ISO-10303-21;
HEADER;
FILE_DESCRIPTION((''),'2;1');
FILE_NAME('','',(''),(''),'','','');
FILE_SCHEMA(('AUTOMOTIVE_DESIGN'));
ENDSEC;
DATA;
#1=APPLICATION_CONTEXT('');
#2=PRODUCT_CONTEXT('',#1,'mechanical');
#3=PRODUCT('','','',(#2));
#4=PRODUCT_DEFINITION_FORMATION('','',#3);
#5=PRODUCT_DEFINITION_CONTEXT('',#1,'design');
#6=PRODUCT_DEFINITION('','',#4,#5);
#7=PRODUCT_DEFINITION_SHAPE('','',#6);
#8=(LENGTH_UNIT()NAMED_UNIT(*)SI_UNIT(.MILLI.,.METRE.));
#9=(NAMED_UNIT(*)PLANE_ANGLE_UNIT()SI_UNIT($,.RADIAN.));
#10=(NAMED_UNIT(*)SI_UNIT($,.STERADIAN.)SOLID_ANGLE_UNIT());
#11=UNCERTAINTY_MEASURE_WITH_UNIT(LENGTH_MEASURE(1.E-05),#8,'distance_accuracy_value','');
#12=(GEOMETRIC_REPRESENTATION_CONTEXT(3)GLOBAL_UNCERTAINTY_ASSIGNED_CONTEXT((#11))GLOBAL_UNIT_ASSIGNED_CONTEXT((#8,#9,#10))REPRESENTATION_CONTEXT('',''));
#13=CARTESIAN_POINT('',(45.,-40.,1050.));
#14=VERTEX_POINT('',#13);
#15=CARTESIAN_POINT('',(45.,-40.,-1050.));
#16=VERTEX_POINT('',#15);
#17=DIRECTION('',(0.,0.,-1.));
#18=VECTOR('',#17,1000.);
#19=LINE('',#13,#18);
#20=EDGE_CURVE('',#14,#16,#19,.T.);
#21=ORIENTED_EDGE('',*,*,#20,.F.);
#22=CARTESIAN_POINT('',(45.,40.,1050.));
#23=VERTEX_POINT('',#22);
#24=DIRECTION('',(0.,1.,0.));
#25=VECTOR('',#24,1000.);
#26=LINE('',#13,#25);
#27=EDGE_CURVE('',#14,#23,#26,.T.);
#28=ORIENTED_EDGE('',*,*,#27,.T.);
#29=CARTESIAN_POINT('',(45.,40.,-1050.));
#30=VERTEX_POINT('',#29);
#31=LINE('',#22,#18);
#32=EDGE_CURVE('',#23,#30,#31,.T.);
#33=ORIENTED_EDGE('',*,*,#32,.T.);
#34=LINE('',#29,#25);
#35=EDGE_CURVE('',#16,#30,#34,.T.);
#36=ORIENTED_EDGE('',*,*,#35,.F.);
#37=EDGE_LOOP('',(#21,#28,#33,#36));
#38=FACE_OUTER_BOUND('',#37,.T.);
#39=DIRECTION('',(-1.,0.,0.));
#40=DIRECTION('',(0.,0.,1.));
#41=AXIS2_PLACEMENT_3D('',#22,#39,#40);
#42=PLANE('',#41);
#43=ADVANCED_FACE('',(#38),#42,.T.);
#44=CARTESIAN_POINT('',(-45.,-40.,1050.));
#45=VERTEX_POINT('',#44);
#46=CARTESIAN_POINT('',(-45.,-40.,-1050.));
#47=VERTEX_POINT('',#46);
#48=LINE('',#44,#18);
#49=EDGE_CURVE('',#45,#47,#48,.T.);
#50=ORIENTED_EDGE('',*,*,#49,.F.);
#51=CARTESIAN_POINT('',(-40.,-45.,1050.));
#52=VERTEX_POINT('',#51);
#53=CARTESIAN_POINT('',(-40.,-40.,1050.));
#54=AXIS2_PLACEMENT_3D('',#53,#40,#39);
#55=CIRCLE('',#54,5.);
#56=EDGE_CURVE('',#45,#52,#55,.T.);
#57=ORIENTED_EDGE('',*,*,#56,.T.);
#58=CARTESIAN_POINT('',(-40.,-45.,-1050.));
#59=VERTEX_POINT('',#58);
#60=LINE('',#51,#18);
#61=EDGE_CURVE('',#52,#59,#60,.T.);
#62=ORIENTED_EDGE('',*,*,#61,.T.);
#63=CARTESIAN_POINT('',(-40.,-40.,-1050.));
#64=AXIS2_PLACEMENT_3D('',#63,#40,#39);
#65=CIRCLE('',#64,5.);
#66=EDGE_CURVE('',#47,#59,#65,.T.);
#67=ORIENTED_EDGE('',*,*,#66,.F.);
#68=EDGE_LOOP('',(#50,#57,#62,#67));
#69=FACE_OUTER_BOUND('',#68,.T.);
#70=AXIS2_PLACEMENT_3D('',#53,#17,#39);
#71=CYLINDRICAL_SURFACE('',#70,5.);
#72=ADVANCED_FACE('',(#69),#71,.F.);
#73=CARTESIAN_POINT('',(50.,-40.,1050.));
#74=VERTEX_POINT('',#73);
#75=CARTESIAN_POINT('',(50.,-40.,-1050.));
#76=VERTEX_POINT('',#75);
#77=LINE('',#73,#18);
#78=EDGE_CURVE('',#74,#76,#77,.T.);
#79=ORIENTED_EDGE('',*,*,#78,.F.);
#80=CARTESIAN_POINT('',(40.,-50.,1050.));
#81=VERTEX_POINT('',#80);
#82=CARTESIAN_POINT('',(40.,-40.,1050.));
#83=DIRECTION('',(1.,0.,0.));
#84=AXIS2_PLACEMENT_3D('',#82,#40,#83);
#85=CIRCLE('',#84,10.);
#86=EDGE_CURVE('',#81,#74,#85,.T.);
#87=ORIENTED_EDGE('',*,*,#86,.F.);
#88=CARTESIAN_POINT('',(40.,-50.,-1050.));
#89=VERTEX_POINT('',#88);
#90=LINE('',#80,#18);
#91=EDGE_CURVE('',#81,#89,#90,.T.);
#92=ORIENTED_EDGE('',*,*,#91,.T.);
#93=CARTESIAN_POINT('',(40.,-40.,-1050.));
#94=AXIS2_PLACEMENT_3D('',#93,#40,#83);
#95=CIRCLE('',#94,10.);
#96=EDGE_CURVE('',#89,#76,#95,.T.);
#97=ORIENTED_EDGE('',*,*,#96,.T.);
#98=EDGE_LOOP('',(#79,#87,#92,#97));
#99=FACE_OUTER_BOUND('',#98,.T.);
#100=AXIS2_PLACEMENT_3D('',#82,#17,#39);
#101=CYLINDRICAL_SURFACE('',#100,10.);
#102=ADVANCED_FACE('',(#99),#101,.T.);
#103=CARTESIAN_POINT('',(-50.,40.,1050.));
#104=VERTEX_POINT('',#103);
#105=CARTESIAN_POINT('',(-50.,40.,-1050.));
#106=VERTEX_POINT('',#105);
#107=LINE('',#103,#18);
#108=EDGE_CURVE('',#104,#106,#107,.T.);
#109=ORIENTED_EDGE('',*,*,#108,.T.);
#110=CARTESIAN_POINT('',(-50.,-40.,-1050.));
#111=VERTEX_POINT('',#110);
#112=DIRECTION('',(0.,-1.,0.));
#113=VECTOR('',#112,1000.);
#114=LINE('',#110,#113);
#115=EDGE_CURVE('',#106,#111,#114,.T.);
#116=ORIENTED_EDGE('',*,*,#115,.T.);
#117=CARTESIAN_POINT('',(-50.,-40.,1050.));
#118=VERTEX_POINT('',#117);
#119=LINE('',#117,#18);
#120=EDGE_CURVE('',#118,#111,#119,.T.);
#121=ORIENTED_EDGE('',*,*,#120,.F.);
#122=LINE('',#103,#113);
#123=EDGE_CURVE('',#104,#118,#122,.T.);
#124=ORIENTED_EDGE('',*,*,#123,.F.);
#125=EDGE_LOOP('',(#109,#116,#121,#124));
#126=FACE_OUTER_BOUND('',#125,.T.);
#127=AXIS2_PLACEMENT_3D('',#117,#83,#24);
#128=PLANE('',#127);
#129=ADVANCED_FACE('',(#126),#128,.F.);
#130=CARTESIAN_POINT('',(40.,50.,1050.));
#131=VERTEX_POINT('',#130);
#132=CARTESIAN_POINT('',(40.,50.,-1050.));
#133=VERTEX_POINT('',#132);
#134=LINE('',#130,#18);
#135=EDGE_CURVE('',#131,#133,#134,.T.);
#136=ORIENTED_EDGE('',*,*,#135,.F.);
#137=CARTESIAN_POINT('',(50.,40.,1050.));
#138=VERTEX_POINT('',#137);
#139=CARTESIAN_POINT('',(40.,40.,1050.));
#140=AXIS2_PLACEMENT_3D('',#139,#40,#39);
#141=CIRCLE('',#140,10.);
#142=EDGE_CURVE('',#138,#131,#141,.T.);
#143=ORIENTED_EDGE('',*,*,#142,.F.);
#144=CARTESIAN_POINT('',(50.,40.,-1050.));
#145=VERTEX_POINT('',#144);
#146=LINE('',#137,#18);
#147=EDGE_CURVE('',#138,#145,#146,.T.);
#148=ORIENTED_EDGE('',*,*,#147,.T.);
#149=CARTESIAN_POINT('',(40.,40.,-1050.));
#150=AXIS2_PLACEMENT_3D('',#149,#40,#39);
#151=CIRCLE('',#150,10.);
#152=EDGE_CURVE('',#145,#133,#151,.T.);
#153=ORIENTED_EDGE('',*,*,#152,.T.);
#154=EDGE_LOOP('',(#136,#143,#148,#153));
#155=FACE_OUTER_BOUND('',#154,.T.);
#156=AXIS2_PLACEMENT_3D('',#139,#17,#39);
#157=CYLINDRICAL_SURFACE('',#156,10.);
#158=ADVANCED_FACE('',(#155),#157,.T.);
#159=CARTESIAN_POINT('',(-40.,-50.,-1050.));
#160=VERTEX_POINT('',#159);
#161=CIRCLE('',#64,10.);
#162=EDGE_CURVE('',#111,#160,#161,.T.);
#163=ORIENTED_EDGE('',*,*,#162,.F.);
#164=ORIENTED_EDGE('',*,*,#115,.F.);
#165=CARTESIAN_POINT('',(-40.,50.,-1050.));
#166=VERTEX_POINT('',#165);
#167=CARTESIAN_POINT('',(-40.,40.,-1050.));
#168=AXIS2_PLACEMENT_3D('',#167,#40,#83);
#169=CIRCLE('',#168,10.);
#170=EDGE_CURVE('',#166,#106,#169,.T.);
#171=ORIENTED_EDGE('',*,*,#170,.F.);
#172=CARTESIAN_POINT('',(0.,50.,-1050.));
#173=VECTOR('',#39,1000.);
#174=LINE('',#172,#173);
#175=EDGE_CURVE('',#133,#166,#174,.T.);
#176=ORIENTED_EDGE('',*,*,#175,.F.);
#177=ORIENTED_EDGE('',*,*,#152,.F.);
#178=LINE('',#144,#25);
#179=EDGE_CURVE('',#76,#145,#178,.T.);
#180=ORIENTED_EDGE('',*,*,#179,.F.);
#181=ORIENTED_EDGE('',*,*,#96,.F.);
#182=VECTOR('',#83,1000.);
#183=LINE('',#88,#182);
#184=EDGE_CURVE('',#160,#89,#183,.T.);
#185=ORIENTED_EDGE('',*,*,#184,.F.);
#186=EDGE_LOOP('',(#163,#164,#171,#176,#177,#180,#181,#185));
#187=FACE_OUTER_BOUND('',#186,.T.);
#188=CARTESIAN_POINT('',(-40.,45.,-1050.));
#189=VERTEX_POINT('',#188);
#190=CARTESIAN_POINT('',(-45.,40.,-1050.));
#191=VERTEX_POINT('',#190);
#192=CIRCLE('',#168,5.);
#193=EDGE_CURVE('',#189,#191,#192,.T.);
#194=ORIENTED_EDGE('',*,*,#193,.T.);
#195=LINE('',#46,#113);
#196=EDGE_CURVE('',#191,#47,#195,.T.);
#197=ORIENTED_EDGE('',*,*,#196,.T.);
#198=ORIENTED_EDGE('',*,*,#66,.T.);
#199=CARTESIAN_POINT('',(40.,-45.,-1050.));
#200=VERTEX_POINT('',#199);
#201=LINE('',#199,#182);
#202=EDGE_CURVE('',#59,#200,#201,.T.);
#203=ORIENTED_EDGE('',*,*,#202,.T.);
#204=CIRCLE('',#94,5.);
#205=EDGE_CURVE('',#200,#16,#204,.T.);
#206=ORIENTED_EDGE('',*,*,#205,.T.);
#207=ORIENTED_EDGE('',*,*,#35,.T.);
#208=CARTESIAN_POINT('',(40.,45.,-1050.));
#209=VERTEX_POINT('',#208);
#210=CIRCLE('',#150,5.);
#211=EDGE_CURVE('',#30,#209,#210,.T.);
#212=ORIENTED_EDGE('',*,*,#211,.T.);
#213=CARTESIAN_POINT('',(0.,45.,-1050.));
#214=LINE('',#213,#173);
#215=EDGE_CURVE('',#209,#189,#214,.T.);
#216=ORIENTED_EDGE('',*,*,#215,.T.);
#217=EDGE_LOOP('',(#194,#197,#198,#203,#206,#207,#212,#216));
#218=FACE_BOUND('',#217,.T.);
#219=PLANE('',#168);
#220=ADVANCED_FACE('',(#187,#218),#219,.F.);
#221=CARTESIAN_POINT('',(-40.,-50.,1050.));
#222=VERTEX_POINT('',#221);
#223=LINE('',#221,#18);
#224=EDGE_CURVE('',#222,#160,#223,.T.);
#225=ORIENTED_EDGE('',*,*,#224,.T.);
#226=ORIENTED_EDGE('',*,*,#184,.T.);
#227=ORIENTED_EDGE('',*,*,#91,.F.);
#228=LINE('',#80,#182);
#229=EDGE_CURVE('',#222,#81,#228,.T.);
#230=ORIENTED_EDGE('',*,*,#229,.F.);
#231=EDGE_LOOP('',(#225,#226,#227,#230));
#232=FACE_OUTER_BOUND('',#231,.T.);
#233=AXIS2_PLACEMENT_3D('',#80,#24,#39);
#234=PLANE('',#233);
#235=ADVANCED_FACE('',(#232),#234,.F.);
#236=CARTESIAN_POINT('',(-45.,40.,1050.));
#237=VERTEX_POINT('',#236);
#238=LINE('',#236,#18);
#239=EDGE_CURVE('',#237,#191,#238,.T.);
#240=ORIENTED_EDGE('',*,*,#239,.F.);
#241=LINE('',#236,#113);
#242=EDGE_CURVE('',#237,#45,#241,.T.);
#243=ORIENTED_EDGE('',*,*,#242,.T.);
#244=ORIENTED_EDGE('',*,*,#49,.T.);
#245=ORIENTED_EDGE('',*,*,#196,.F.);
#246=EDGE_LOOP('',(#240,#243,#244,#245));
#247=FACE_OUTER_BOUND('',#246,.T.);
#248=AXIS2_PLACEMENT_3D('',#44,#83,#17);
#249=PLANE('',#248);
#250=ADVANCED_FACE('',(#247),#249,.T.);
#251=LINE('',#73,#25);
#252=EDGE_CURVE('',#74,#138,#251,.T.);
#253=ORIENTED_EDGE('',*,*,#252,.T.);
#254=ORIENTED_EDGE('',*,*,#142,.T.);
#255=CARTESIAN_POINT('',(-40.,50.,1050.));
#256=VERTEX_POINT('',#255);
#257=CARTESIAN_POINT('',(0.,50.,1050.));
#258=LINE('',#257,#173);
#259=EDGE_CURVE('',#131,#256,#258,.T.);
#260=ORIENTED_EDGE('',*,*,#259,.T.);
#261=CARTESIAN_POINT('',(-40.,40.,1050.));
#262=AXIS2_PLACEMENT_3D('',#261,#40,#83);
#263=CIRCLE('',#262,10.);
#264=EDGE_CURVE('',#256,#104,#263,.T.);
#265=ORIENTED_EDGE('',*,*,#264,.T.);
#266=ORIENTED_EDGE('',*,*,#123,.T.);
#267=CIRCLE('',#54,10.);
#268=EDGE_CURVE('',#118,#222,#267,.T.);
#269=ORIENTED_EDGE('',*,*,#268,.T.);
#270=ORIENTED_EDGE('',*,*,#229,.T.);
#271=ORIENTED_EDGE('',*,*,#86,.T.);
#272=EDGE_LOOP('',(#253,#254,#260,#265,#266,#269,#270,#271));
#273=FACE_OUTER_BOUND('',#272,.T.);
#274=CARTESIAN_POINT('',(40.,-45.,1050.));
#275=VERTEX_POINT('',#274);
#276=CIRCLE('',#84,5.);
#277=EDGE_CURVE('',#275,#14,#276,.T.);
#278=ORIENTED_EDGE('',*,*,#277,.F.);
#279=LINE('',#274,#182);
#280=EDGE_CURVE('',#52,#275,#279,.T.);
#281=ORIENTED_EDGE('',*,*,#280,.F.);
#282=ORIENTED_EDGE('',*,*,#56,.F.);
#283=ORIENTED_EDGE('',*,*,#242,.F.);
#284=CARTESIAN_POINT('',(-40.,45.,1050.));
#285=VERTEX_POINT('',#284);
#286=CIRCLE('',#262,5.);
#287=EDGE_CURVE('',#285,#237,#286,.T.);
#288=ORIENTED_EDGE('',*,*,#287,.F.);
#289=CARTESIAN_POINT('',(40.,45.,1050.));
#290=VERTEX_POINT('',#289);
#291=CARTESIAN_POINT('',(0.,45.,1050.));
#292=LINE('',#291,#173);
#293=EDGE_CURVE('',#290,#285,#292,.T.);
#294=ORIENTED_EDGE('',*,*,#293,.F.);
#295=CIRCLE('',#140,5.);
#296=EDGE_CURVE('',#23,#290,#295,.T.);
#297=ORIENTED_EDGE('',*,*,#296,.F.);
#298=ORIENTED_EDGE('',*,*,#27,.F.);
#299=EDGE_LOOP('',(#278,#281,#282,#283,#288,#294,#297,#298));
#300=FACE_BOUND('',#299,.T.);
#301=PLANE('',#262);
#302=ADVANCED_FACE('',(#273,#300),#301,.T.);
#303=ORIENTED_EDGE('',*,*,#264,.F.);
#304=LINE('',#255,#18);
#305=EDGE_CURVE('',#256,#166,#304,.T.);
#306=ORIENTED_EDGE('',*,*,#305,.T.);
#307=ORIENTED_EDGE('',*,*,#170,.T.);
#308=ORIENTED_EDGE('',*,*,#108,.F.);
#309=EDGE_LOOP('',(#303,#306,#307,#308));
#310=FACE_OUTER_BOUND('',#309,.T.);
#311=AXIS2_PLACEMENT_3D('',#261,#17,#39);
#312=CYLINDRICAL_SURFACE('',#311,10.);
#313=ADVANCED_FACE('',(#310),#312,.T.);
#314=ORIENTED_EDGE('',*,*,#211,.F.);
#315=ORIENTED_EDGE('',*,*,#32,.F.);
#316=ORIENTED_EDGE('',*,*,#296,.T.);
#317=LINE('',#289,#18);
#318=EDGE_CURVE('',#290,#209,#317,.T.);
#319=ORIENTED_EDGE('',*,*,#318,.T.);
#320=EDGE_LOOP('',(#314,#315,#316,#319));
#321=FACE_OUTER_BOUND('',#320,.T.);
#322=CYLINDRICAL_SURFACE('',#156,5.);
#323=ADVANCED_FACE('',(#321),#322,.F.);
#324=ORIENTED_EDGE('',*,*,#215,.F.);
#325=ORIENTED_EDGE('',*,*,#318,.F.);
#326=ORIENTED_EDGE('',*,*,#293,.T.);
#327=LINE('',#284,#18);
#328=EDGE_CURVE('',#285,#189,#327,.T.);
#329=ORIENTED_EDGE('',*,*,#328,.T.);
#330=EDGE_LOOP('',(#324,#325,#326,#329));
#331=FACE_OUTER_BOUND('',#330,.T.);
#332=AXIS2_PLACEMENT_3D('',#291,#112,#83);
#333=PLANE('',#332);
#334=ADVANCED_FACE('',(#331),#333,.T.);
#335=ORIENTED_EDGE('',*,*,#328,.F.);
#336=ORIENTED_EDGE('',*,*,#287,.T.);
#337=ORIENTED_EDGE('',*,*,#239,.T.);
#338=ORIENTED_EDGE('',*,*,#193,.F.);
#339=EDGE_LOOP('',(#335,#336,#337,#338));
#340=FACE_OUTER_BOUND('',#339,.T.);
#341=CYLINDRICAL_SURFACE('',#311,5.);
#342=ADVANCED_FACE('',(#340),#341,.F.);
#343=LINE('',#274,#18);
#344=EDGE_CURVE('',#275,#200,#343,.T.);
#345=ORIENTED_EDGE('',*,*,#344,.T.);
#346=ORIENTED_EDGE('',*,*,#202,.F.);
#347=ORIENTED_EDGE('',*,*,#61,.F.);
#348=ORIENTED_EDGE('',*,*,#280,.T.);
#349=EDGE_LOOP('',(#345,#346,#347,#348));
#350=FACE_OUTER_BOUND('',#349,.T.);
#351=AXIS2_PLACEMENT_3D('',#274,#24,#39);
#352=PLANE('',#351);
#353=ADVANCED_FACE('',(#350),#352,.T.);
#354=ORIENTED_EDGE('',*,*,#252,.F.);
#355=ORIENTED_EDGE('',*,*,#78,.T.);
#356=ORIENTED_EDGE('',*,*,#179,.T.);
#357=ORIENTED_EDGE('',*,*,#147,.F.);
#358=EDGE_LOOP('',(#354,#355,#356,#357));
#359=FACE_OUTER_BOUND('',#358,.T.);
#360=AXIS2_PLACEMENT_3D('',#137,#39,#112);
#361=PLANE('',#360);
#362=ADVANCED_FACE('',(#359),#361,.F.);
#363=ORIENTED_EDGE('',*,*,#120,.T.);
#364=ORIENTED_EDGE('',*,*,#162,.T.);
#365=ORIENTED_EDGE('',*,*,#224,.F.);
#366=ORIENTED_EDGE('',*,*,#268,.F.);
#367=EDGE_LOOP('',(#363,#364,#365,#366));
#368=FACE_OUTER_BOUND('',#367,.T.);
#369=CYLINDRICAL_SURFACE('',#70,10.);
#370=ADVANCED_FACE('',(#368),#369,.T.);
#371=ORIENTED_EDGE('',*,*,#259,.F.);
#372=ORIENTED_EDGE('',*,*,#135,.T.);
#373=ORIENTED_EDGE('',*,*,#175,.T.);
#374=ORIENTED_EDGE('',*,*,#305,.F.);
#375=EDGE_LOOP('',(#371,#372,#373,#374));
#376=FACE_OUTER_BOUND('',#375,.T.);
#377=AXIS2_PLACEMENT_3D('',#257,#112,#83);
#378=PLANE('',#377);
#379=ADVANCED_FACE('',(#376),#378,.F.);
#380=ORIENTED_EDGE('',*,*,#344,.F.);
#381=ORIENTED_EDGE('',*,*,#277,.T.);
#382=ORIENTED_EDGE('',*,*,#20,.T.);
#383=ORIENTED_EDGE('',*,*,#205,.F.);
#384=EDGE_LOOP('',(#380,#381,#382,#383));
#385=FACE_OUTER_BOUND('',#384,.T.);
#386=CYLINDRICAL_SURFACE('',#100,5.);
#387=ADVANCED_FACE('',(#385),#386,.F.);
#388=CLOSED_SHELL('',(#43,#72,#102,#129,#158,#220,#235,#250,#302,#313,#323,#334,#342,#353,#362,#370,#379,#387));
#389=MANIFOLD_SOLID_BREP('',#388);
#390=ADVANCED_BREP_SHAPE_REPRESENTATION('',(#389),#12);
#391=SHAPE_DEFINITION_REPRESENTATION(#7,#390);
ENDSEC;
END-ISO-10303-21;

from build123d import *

# Parameters (mm, degrees)
BOSS_EXTRUDE_1_DEPTH = 1050


with BuildPart() as part:
    # Sketch 1 → Boss-Extrude 1 (new, symmetric)
    with BuildSketch(Plane.XY):
        with BuildLine():
            Line((0, 50), (-40, 50))
            ThreePointArc((-40, 50), (-47.071067812, 47.071067812), (-50, 40))
            Line((-50, 40), (-50, 0))
            Line((-50, 0), (-50, -40))
            ThreePointArc((-50, -40), (-47.071067812, -47.071067812), (-40, -50))
            Line((-40, -50), (40, -50))
            ThreePointArc((40, -50), (47.071067812, -47.071067812), (50, -40))
            Line((50, -40), (50, 0))
            Line((50, 0), (50, 40))
            ThreePointArc((50, 40), (47.071067812, 47.071067812), (40, 50))
            Line((40, 50), (0, 50))
        make_face()
        with BuildLine():
            Line((0, 45), (-40, 45))
            ThreePointArc((-40, 45), (-43.535533906, 43.535533906), (-45, 40))
            Line((-45, 40), (-45, 0))
            Line((-45, 0), (-45, -40))
            ThreePointArc((-45, -40), (-43.535533906, -43.535533906), (-40, -45))
            Line((-40, -45), (40, -45))
            ThreePointArc((40, -45), (43.535533906, -43.535533906), (45, -40))
            Line((45, -40), (45, 0))
            Line((45, 0), (45, 40))
            ThreePointArc((45, 40), (43.535533906, 43.535533906), (40, 45))
            Line((40, 45), (0, 45))
        make_face(mode=Mode.SUBTRACT)
    extrude(amount=BOSS_EXTRUDE_1_DEPTH, both=True)


solid = part.part
